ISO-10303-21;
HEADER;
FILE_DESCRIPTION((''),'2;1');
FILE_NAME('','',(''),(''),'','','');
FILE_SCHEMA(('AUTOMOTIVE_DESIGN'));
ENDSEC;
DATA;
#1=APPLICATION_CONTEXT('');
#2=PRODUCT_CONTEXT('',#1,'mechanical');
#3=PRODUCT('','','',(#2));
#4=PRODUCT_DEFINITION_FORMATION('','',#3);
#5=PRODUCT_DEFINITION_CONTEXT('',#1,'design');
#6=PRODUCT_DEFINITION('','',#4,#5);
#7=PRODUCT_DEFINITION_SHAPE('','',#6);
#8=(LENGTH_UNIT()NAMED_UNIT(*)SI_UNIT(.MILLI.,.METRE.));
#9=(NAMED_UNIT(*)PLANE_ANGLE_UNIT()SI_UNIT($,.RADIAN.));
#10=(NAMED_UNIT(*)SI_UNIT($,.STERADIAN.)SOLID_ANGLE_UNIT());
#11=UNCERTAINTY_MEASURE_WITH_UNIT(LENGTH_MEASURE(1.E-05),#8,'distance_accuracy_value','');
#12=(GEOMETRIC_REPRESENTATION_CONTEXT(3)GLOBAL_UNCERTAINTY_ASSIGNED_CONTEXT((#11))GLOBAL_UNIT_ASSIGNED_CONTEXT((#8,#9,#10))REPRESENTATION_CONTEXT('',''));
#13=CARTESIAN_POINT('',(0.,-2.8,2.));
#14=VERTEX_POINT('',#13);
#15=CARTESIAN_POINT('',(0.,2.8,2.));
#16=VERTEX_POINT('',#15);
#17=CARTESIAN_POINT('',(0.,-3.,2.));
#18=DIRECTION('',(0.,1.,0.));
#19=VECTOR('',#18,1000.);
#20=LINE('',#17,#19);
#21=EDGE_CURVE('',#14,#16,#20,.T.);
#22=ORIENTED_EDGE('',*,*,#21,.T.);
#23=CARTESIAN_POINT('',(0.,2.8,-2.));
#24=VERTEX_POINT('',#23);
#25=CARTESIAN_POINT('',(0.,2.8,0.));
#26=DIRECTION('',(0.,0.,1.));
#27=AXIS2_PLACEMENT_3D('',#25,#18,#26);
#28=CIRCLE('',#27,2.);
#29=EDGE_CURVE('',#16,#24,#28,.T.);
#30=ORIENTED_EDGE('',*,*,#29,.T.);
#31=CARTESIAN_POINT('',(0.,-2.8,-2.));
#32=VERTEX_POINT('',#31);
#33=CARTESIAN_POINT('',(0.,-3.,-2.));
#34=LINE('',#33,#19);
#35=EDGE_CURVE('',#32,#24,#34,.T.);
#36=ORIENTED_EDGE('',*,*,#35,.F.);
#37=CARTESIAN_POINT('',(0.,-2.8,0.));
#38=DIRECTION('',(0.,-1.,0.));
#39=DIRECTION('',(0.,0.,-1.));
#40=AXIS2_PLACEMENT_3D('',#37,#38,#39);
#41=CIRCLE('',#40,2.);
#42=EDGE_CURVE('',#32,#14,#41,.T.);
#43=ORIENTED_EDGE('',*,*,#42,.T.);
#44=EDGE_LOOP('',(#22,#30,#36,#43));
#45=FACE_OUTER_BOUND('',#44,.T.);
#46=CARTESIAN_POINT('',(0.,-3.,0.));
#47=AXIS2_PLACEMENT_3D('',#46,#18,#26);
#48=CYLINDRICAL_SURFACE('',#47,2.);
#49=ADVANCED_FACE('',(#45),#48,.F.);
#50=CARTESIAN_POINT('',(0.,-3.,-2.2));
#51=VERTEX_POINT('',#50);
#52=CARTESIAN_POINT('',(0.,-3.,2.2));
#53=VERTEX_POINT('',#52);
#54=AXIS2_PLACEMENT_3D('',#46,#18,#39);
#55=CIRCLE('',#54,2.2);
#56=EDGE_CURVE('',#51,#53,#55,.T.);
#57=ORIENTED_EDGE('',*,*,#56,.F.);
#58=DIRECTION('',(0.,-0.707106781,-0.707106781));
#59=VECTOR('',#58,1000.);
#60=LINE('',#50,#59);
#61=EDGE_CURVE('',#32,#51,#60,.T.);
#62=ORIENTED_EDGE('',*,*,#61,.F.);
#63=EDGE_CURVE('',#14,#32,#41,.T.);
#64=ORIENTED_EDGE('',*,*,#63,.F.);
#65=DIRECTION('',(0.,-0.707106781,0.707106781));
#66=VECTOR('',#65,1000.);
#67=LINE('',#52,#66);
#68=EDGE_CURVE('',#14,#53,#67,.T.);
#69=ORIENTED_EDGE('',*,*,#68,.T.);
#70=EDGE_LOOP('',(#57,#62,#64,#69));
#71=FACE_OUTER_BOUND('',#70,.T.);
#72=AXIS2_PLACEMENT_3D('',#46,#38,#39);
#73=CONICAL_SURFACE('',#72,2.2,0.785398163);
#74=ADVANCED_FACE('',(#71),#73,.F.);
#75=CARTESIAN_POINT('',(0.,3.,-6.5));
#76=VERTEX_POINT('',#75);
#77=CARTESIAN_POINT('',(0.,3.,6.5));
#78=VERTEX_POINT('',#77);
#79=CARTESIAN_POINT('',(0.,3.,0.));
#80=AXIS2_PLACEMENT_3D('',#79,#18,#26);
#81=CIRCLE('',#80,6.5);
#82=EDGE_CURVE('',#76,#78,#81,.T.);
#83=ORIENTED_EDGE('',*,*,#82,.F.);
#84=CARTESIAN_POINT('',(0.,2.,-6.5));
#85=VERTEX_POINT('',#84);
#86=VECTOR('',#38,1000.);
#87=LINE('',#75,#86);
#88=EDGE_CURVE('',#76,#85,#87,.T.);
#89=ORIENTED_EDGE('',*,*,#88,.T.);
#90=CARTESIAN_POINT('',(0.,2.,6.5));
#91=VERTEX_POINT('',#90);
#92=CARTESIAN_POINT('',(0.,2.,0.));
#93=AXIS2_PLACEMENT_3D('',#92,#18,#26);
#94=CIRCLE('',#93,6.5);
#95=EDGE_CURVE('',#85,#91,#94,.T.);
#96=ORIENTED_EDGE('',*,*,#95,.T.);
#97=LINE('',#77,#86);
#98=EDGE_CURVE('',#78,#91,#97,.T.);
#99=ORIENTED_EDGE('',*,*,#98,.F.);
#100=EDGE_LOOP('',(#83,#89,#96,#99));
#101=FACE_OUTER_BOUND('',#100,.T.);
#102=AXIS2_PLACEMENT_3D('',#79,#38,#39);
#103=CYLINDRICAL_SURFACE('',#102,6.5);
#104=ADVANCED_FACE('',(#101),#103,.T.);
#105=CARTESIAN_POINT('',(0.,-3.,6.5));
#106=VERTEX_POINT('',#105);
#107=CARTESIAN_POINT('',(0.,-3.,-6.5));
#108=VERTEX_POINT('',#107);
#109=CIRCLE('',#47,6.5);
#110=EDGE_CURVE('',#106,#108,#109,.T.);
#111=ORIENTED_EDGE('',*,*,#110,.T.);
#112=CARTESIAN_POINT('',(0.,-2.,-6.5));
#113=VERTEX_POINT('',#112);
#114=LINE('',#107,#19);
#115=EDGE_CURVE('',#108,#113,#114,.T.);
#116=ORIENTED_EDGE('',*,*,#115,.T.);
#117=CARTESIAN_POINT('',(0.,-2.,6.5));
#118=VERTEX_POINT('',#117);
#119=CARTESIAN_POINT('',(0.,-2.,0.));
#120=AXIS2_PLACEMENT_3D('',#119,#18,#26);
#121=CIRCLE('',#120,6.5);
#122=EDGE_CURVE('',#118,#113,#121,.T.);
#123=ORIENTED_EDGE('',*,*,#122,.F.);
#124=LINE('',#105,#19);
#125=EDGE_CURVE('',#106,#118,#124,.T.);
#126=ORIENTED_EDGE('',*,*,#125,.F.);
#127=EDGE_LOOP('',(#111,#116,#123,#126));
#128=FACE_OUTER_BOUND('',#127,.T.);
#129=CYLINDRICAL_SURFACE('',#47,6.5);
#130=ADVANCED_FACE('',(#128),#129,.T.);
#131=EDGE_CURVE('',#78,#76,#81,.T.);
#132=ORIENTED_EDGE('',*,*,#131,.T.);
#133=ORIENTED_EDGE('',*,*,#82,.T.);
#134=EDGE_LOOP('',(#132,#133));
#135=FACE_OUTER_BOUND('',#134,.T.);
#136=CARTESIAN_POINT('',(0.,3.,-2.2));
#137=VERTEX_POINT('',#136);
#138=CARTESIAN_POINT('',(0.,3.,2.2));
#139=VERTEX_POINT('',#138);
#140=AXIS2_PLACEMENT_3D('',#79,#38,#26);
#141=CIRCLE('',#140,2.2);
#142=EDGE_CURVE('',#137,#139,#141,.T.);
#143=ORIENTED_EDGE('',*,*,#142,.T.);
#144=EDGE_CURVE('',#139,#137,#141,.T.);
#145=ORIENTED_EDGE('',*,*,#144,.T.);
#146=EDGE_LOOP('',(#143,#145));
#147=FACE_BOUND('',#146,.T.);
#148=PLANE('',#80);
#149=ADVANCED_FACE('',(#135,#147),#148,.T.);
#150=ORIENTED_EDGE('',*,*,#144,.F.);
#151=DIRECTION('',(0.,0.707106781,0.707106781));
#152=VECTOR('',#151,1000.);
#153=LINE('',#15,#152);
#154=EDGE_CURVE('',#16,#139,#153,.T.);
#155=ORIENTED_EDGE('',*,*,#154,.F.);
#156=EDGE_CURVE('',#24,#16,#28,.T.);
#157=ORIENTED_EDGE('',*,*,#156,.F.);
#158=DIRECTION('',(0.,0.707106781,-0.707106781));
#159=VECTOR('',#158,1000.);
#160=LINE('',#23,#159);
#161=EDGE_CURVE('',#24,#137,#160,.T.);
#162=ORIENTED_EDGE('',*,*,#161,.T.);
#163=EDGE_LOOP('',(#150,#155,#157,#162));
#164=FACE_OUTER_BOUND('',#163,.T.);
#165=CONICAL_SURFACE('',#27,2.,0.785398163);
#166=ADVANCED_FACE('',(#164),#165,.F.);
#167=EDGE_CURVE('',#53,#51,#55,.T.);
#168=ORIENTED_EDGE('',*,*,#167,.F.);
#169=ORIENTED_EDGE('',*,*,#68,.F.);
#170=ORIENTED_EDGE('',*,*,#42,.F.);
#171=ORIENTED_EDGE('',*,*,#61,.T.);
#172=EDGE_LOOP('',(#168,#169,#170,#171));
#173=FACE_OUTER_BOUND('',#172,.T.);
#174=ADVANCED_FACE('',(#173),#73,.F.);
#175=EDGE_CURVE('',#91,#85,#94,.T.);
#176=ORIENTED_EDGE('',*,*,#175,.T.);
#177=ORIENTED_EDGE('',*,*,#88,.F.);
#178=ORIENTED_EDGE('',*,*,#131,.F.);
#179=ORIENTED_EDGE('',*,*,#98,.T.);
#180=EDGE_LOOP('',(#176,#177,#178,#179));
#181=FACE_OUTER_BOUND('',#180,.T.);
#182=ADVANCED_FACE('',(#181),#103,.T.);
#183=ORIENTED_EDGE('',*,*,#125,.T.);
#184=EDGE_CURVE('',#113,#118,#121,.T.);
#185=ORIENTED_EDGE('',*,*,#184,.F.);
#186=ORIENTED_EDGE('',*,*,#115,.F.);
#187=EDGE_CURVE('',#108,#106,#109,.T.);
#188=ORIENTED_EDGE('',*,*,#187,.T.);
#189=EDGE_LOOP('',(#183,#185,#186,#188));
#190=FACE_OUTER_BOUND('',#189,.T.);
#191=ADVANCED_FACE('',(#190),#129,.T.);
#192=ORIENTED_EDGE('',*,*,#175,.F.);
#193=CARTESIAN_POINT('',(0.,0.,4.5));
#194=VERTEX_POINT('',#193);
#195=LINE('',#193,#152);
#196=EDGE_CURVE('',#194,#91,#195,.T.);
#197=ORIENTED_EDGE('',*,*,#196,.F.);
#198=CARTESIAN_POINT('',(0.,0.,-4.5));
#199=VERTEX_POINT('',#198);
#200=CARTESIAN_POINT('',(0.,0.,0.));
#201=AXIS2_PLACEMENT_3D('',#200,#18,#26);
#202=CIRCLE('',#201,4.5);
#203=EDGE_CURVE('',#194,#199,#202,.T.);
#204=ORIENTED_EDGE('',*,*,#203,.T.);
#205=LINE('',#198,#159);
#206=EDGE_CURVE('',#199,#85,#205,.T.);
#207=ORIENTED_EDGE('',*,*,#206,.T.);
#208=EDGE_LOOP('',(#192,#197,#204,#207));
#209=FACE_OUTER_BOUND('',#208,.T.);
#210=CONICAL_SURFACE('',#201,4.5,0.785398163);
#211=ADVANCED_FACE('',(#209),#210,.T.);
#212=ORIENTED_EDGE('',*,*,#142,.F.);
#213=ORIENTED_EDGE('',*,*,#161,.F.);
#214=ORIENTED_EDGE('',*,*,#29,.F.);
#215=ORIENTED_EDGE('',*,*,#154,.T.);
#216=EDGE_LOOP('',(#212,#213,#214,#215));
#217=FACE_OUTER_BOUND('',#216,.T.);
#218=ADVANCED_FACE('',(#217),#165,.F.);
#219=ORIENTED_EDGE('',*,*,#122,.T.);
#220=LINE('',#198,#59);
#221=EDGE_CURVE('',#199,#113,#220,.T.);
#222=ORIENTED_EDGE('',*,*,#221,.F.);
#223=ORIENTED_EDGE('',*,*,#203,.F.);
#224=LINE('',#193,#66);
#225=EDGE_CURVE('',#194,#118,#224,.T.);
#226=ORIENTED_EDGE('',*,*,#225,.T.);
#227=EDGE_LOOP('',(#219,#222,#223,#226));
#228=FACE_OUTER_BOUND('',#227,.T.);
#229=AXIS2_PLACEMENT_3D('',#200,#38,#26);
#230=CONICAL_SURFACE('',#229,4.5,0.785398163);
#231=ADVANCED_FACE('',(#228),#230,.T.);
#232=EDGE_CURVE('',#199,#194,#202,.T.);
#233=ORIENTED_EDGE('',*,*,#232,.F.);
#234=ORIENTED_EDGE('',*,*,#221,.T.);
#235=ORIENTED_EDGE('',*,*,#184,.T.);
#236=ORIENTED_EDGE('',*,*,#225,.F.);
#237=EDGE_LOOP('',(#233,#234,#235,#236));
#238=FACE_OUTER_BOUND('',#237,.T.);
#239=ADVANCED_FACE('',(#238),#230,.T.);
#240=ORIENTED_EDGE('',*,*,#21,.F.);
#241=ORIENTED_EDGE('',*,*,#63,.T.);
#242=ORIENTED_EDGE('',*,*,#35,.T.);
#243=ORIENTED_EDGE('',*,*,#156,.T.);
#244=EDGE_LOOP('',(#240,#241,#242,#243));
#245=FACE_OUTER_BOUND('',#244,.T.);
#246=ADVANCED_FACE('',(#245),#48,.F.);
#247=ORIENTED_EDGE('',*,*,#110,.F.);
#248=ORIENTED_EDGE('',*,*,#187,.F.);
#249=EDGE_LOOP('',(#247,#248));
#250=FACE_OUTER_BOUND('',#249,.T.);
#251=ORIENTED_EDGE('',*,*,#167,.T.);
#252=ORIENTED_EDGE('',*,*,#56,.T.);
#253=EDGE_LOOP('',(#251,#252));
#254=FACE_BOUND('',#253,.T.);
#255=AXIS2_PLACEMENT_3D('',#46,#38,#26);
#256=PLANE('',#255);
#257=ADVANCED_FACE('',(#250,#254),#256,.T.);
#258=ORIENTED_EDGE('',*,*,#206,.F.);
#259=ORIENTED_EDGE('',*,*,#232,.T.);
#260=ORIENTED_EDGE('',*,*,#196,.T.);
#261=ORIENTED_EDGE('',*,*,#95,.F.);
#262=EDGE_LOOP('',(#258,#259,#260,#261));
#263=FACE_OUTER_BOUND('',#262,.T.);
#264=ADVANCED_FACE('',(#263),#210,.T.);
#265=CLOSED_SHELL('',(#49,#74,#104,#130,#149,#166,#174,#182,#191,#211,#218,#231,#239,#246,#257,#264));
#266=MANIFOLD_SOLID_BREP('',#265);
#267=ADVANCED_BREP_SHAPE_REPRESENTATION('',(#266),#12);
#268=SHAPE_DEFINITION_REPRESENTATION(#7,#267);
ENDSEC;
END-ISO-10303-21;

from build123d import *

# Parameters (mm, degrees)
SKETCH_1_R          = 4.5
SKETCH_2_R          = 6.5
SKETCH_3_R          = 6.5
EXTRUDE_1_DEPTH     = 1
SKETCH_4_R          = 2
CUT_EXTRUDE_1_DEPTH = 11.977249318
CHAMFER_1_SIZE      = 0.2


with BuildPart() as part:
    # 草图1 → 放样1 section 0
    with BuildSketch(Plane(origin=(0, 0, 0), x_dir=(1, 0, 0), z_dir=(0, 1, 0))):
        Circle(SKETCH_1_R)
    # 草图2 → 放样1 section 1
    with BuildSketch(Plane(origin=(0, 2, 0), x_dir=(1, 0, 0), z_dir=(0, 1, 0))):
        Circle(SKETCH_2_R)
    loft_1 = loft()

    # 草图3 → 凸台-拉伸1 (add)
    with BuildSketch(Plane(origin=(0, 2, 0), x_dir=(1, 0, 0), z_dir=(0, 1, 0))):
        with Locations(Location((0, 0, 0), (0, 0, 270))):
            Circle(SKETCH_3_R)
    extrude_1 = extrude(amount=EXTRUDE_1_DEPTH)

    # 镜向1: 放样1, 凸台-拉伸1 across plane
    add(loft_1.mirror(Plane.ZX))
    add(extrude_1.mirror(Plane.ZX))

    # 草图4 → 切除-拉伸1 (cut, through all)
    with BuildSketch(Plane(origin=(0, 3, 0), x_dir=(1, 0, 0), z_dir=(0, 1, 0))):
        with Locations(Location((0, 0, 0), (0, 0, 270))):
            Circle(SKETCH_4_R)
    extrude(amount=-CUT_EXTRUDE_1_DEPTH, mode=Mode.SUBTRACT)

    # 倒角1
    chamfer_1_edges = [part.edges().sort_by_distance(p)[0] for p in [
        (0, -3, -2),
        (0, 3, -2),
    ]]
    chamfer(chamfer_1_edges, length=CHAMFER_1_SIZE)


solid = part.part
